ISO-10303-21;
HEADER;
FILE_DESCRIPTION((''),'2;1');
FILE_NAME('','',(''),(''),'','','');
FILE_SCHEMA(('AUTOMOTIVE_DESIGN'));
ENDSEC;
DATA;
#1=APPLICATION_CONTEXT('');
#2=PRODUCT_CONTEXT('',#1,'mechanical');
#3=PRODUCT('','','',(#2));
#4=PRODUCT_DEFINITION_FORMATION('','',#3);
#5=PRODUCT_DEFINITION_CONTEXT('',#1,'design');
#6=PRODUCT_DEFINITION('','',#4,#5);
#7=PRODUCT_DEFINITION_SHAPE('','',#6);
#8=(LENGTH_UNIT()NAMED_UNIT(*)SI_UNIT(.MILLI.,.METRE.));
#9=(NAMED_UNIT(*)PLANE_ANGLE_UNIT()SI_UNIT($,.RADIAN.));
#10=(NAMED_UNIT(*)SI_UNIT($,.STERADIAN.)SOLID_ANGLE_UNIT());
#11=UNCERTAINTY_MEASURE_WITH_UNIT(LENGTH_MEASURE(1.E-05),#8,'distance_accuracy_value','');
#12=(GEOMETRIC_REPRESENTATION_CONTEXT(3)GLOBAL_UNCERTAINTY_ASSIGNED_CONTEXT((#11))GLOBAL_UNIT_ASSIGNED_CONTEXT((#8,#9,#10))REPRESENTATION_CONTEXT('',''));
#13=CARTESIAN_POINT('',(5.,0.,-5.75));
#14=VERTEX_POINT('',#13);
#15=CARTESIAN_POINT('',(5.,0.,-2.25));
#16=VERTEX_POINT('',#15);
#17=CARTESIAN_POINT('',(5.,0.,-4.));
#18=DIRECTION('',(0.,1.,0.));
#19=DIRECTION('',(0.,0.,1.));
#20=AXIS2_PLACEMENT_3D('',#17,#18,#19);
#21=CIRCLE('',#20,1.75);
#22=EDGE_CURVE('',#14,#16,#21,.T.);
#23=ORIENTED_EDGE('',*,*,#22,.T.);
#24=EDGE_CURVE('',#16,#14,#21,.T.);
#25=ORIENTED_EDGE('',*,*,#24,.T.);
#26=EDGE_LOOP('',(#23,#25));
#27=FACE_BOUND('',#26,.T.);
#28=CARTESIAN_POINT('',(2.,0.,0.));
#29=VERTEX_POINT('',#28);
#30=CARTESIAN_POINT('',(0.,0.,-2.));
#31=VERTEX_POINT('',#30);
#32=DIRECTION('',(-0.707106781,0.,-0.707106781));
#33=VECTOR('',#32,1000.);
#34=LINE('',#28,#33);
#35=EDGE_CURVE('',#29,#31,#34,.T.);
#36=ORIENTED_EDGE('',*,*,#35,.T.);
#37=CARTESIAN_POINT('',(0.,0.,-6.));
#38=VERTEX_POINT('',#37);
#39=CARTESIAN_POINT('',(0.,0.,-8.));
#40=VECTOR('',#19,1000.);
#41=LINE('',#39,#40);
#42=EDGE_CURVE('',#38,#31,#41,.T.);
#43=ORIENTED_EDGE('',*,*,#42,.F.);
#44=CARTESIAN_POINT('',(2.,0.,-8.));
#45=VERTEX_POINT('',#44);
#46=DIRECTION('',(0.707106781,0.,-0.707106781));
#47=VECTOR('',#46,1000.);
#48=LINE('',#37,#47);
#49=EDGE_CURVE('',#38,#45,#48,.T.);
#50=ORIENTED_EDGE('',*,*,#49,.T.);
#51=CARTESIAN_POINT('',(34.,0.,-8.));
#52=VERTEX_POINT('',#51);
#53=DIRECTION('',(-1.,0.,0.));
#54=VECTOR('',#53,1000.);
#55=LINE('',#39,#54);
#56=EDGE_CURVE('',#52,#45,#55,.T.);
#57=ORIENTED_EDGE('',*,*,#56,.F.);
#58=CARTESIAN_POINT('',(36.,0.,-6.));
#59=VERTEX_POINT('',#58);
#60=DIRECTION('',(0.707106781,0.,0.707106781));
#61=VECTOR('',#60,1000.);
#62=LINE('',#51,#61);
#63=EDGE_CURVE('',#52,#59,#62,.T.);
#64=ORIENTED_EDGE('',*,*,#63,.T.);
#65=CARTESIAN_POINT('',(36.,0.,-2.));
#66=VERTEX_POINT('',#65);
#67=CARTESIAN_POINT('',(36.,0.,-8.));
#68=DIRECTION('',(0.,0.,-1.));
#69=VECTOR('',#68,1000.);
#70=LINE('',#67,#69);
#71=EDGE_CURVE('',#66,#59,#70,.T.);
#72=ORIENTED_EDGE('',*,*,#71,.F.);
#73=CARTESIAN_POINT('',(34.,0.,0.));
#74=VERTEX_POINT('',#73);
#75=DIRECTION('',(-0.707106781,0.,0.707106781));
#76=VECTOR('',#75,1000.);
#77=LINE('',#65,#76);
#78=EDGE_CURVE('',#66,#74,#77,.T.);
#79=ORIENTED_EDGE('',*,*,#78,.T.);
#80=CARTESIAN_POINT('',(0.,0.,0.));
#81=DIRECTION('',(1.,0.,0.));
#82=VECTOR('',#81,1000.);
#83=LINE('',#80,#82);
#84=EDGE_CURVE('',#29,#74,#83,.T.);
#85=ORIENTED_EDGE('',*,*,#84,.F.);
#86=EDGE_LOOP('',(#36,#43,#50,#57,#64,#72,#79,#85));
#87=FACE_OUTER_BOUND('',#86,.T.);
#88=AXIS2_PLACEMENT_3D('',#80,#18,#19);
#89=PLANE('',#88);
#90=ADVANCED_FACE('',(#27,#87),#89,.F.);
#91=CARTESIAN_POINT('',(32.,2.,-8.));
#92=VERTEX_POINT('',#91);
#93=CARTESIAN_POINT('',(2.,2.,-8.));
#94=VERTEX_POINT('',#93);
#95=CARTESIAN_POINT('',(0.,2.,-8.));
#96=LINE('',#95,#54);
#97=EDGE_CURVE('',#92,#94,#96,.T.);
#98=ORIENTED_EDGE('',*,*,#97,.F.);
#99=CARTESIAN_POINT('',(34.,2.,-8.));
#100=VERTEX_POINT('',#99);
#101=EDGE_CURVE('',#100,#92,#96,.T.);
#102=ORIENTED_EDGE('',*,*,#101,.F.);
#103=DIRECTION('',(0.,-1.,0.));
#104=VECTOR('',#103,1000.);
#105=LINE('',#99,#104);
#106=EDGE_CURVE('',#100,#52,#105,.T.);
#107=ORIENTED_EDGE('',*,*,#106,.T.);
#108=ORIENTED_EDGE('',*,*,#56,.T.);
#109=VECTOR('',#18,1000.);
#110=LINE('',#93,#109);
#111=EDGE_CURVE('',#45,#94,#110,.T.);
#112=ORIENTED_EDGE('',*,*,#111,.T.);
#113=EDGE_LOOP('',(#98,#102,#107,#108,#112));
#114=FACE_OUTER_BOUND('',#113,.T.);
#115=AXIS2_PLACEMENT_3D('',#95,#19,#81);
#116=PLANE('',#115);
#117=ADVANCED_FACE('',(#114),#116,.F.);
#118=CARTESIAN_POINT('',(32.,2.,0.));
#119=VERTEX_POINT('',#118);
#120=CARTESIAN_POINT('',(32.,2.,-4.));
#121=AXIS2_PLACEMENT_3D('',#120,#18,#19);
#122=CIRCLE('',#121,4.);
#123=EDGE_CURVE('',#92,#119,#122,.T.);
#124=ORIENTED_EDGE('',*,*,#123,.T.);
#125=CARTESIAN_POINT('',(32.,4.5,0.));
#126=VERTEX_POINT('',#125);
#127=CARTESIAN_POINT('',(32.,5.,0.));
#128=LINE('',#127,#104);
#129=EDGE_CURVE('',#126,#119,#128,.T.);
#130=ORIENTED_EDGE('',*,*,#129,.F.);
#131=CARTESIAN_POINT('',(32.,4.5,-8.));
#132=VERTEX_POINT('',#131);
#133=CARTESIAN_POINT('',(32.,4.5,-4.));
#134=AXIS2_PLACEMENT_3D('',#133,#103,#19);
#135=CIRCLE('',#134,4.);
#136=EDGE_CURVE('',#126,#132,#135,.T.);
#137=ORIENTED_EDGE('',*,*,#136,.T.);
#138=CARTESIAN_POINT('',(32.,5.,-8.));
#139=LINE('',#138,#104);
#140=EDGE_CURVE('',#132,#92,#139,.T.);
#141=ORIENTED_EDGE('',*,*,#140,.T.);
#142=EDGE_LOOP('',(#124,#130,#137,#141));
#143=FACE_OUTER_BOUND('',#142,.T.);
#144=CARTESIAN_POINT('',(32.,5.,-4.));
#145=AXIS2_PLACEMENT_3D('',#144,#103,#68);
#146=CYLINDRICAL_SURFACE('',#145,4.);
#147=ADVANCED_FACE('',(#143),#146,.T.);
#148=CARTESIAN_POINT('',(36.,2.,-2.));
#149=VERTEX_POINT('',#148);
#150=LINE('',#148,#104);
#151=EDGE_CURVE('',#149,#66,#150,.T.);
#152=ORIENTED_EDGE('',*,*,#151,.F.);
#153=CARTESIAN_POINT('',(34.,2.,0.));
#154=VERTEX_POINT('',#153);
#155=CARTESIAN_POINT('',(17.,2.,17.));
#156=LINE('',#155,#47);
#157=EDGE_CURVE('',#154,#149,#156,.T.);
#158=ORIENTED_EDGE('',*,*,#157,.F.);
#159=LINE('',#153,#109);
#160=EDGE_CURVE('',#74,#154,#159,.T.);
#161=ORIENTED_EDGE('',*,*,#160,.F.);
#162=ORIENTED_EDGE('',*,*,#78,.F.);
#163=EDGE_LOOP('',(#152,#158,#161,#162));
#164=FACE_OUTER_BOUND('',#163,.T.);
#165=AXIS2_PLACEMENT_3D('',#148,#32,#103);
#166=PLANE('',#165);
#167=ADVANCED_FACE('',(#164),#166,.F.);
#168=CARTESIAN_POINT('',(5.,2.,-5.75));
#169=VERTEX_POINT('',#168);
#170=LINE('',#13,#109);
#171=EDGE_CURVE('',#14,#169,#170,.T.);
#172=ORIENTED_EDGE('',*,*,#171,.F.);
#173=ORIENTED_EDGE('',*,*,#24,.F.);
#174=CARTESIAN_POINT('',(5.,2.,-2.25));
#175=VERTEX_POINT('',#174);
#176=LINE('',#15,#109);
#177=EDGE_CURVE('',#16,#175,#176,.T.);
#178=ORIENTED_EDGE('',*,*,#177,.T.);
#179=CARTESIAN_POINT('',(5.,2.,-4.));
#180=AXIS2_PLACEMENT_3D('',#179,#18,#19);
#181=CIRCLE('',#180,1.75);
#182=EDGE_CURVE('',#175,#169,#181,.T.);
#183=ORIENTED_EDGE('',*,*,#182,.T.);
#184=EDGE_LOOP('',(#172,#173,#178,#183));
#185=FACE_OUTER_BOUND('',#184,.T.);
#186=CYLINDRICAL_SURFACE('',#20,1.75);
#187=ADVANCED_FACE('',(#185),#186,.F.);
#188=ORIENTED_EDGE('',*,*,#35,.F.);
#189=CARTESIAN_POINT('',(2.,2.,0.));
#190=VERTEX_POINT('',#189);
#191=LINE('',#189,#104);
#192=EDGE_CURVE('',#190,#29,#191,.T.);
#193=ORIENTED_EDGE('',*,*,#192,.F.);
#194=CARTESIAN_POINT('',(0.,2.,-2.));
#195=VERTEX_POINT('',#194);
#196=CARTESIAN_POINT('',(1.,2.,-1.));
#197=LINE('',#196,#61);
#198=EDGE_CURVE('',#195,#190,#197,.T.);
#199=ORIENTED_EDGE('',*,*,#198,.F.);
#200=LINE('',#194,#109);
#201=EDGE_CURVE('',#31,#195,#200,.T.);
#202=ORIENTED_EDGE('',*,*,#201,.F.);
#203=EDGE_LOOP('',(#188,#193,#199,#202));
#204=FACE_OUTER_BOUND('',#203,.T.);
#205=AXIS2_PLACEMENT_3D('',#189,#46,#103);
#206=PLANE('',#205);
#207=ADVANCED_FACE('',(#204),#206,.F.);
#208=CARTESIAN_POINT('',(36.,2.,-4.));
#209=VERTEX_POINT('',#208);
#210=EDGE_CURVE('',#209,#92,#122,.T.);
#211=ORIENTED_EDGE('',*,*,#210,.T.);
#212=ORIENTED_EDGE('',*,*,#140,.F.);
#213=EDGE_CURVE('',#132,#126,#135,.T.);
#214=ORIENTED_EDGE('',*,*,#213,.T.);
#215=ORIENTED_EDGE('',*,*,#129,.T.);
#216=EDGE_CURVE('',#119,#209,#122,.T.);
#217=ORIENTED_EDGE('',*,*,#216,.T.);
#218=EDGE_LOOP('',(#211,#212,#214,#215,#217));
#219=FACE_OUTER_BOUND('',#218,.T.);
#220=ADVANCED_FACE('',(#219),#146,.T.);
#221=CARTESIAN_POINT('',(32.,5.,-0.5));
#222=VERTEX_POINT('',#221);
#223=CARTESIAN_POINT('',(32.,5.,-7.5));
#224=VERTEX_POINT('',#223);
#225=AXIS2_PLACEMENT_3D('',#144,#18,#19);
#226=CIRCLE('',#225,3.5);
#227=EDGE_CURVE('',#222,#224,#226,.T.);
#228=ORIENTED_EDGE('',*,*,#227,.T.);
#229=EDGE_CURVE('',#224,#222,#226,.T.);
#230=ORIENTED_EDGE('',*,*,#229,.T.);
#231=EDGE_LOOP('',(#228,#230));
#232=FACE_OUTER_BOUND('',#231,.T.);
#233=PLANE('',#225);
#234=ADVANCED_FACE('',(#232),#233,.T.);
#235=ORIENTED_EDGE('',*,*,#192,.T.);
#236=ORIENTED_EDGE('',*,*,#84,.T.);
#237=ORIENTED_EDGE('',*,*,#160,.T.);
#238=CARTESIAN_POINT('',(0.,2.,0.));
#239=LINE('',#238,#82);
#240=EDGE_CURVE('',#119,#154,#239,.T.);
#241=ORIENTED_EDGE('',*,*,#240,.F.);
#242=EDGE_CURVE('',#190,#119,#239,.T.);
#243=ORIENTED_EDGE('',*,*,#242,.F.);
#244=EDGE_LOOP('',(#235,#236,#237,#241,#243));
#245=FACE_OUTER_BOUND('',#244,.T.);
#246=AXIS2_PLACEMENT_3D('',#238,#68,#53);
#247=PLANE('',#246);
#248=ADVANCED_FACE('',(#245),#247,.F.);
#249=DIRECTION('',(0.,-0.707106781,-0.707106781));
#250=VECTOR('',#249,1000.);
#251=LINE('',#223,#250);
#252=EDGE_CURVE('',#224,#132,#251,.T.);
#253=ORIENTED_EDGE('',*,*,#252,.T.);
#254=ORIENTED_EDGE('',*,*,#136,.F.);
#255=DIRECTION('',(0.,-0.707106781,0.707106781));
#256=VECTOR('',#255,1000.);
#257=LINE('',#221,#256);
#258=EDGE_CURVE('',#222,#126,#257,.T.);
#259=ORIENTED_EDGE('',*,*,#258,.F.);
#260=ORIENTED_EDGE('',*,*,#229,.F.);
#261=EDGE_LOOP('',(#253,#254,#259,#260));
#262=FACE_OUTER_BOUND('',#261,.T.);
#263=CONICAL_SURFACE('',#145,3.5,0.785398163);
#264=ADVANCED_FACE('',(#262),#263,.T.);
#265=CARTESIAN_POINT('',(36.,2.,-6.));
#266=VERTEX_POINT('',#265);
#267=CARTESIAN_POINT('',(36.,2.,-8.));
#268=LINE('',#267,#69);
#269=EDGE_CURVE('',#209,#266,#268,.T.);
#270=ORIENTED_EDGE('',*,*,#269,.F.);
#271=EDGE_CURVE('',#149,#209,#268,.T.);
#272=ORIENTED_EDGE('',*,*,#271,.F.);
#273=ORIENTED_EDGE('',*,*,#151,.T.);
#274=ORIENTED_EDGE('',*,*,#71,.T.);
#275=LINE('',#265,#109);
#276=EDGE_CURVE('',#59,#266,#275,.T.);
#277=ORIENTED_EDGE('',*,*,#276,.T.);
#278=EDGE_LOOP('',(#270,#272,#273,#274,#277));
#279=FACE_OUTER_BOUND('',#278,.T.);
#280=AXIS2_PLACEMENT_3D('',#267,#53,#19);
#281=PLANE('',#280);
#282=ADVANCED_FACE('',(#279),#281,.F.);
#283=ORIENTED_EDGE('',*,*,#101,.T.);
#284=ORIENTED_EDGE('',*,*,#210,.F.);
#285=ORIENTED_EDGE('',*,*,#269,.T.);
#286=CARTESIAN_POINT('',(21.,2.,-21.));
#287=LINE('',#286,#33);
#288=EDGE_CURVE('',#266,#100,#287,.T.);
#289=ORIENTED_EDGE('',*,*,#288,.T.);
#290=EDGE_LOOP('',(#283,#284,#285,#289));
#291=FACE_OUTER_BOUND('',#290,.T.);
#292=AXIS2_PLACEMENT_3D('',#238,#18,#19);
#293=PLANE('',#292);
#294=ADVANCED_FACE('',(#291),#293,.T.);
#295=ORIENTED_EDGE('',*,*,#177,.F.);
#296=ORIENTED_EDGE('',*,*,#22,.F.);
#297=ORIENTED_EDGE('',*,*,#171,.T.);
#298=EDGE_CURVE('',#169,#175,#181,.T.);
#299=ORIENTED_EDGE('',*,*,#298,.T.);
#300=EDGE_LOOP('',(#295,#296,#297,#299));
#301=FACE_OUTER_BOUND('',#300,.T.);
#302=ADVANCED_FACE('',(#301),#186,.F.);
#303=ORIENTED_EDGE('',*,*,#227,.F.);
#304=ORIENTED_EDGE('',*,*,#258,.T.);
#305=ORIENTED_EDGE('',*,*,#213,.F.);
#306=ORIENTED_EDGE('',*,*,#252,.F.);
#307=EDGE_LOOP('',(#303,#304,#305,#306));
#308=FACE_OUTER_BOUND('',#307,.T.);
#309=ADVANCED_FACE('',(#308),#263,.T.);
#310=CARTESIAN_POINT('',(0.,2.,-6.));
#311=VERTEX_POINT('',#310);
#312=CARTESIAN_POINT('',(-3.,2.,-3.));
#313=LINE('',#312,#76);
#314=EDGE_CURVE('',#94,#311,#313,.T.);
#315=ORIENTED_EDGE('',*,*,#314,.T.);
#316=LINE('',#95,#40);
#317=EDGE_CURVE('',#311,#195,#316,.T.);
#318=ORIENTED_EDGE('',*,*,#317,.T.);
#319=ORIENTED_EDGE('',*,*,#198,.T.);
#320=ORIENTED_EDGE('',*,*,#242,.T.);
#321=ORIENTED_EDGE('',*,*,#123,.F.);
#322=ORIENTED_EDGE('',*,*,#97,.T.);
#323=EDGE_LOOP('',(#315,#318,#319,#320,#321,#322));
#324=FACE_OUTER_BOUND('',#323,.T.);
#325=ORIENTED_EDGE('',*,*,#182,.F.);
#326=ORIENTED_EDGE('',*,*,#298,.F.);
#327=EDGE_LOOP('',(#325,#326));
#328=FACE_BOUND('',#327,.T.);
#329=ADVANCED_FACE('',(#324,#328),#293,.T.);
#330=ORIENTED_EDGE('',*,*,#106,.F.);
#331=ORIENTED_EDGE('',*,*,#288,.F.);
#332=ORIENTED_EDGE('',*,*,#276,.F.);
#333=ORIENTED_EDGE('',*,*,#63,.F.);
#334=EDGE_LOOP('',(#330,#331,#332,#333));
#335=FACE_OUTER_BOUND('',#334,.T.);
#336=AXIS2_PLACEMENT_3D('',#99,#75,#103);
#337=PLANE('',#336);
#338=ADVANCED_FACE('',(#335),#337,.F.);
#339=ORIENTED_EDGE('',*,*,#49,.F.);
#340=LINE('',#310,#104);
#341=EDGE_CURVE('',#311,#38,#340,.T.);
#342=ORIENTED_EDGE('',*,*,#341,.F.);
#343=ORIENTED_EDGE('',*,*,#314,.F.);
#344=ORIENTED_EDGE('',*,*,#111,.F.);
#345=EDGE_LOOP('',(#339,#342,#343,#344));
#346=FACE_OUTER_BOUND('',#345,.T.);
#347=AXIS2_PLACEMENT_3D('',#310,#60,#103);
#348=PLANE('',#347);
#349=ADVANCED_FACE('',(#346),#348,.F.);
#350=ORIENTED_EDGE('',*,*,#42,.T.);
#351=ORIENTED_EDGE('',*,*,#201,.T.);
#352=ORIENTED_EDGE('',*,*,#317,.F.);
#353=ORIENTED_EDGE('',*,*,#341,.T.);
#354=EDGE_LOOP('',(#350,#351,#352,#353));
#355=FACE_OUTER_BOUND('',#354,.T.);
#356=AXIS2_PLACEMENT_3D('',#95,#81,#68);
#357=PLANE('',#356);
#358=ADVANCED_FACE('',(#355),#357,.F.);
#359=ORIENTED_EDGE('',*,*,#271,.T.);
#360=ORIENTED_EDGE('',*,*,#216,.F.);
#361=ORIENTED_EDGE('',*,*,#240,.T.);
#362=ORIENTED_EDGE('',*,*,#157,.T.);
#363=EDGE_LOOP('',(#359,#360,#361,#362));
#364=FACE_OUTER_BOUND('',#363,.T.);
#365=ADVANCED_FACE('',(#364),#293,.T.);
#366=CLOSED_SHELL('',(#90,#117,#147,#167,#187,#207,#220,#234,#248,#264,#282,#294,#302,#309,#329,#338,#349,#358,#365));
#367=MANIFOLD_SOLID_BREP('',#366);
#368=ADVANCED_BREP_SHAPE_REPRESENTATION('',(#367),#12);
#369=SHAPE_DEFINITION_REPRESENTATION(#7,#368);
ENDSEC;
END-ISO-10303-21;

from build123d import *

# Parameters (mm, degrees)
SKETCH1_W           = 36
SKETCH1_H           = 8
BOSS_EXTRUDE1_DEPTH = 2
SKETCH2_R           = 1.75
CUT_EXTRUDE1_DEPTH  = 37.932370625
SKETCH3_R           = 4
BOSS_EXTRUDE2_DEPTH = 3
CHAMFER1_SIZE       = 0.5
CHAMFER2_SIZE       = 2


with BuildPart() as part:
    # Sketch1 → Boss-Extrude1 (new body)
    with BuildSketch(Plane(origin=(0, 0, 0), x_dir=(1, 0, 0), z_dir=(0, 1, 0))):
        with Locations((18, 4)):
            Rectangle(SKETCH1_W, SKETCH1_H)
    extrude(amount=BOSS_EXTRUDE1_DEPTH)

    # Sketch2 → Cut-Extrude1 (cut, through all)
    with BuildSketch(Plane(origin=(0, 2, 0), x_dir=(1, 0, 0), z_dir=(0, 1, 0))):
        with Locations(Location((5, 4, 0), (0, 0, 270))):
            Circle(SKETCH2_R)
    extrude(amount=-CUT_EXTRUDE1_DEPTH, mode=Mode.SUBTRACT)

    # Sketch3 → Boss-Extrude2 (add)
    with BuildSketch(Plane(origin=(0, 2, 0), x_dir=(1, 0, 0), z_dir=(0, 1, 0))):
        with Locations(Location((32, 4, 0), (0, 0, 270))):
            Circle(SKETCH3_R)
    extrude(amount=BOSS_EXTRUDE2_DEPTH)

    # Chamfer1
    chamfer1_edges = [part.edges().sort_by_distance(p)[0] for p in [
        (32, 5, -8),
    ]]
    chamfer(chamfer1_edges, length=CHAMFER1_SIZE)

    # Chamfer2
    chamfer2_edges = [part.edges().sort_by_distance(p)[0] for p in [
        (0, 1, -8),
        (36, 1, -8),
        (36, 1, 0),
        (0, 1, 0),
    ]]
    chamfer(chamfer2_edges, length=CHAMFER2_SIZE)


solid = part.part
